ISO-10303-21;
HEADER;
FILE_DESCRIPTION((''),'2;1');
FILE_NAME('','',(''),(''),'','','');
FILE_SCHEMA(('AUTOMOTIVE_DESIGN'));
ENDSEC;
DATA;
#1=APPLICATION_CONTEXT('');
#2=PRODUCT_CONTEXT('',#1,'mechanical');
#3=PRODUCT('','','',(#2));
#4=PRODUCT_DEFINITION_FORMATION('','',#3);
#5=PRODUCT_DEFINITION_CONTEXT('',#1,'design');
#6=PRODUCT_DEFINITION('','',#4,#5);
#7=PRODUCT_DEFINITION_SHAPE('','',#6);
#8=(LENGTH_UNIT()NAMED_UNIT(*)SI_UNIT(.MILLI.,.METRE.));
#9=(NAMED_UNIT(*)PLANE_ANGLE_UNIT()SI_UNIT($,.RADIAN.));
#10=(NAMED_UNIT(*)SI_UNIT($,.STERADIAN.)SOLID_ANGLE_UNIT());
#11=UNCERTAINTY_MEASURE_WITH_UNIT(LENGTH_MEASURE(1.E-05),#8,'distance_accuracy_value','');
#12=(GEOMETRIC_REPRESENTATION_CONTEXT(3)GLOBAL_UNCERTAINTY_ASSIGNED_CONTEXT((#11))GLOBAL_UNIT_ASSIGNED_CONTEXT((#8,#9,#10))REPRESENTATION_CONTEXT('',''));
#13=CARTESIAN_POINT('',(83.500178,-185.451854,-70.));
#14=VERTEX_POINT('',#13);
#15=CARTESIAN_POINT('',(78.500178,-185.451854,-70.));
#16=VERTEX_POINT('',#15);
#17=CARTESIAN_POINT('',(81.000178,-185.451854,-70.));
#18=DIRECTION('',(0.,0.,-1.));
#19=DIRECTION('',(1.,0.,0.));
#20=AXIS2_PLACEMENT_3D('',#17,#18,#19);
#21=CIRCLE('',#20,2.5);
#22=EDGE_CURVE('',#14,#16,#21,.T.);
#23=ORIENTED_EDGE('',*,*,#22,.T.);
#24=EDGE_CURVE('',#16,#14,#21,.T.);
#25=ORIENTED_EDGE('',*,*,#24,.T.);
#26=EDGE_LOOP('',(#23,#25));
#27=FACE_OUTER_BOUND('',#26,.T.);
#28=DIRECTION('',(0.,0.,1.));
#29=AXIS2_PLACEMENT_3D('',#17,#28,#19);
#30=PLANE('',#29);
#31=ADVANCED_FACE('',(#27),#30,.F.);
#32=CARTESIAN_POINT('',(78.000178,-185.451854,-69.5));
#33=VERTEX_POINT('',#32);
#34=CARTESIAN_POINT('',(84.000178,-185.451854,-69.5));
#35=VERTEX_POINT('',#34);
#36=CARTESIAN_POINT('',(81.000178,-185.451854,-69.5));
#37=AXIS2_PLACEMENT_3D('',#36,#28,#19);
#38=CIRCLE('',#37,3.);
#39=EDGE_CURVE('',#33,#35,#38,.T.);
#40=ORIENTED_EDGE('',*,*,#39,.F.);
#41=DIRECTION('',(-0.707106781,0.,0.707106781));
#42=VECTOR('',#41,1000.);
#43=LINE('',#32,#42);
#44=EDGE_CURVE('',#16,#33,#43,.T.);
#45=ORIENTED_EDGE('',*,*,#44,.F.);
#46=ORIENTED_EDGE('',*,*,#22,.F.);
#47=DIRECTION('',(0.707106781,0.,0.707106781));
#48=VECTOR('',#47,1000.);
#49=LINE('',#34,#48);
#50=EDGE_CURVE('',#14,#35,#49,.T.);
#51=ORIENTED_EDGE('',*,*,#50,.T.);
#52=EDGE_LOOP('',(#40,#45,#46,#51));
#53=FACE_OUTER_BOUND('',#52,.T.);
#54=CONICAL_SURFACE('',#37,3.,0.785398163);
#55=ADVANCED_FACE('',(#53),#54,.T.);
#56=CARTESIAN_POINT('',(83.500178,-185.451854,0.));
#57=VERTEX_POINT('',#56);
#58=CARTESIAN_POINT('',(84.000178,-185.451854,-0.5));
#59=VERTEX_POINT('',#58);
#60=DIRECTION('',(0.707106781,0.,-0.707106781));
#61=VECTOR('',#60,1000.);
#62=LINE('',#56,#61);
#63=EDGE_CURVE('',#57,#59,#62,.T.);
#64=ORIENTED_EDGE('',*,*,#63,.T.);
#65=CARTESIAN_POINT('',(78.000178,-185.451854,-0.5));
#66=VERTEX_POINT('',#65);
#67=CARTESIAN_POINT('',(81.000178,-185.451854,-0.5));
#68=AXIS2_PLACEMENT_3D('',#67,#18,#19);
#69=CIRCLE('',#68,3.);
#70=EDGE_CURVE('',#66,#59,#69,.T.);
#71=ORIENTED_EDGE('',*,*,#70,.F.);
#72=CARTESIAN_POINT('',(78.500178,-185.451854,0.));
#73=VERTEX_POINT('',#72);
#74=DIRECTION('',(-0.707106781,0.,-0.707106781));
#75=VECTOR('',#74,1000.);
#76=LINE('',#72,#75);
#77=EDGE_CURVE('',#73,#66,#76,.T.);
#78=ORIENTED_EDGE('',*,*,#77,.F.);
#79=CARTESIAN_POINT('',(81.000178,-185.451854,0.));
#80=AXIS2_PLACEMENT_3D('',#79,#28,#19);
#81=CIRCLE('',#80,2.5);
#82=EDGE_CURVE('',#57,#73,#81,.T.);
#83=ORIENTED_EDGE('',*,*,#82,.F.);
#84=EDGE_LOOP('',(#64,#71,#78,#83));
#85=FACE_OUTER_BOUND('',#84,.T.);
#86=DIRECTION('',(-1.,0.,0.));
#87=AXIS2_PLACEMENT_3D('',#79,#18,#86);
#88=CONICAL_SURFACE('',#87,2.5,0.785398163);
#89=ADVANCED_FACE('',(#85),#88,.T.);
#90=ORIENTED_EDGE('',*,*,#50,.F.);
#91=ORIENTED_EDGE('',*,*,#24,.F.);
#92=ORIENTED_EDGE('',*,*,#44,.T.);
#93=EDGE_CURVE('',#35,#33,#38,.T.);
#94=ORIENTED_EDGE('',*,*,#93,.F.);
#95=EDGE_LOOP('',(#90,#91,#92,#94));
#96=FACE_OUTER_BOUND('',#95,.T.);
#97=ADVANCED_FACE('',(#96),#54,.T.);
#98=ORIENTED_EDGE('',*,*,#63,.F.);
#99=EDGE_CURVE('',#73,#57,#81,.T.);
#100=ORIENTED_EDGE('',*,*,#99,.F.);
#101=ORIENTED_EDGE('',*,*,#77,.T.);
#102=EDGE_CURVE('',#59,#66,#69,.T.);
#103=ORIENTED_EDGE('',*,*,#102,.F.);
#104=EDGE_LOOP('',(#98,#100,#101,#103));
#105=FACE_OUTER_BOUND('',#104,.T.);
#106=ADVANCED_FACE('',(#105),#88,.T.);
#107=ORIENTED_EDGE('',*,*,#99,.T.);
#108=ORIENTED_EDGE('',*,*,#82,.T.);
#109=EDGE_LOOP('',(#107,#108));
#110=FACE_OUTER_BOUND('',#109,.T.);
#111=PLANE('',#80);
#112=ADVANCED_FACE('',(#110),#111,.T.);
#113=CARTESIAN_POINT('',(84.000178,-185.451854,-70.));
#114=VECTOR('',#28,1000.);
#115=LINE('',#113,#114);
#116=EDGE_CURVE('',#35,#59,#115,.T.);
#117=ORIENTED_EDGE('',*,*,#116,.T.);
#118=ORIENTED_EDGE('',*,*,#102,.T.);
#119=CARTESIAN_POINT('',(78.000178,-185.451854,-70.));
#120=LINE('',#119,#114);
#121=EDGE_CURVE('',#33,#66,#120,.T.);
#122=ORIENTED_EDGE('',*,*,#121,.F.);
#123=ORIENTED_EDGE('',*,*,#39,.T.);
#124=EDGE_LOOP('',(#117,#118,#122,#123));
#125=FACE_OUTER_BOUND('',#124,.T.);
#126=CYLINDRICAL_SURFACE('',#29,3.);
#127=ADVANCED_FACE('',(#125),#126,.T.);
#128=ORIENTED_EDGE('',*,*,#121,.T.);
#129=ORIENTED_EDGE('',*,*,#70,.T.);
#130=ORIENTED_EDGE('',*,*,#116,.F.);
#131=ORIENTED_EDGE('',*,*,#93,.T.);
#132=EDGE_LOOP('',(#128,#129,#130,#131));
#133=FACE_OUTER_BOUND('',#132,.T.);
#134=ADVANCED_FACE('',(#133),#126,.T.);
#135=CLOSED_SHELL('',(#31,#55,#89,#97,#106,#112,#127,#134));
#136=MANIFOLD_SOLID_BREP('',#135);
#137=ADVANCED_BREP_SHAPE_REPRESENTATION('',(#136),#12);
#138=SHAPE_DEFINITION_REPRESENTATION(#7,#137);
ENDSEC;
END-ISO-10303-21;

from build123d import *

# Parameters (mm, degrees)
SKETCH1_R           = 3
BOSS_EXTRUDE1_DEPTH = 70
CHAMFER1_SIZE       = 0.5


with BuildPart() as part:
    # Sketch1 → Boss-Extrude1 (new body)
    with BuildSketch(Plane.XY):
        with Locations((81.000178314, -185.451853844)):
            Circle(SKETCH1_R)
    extrude(amount=-BOSS_EXTRUDE1_DEPTH)

    # Chamfer1
    chamfer1_edges = [part.edges().sort_by_distance(p)[0] for p in [
        (78.000178314, -185.451853844, 0),
        (78.000178314, -185.451853844, -70),
    ]]
    chamfer(chamfer1_edges, length=CHAMFER1_SIZE)


solid = part.part
